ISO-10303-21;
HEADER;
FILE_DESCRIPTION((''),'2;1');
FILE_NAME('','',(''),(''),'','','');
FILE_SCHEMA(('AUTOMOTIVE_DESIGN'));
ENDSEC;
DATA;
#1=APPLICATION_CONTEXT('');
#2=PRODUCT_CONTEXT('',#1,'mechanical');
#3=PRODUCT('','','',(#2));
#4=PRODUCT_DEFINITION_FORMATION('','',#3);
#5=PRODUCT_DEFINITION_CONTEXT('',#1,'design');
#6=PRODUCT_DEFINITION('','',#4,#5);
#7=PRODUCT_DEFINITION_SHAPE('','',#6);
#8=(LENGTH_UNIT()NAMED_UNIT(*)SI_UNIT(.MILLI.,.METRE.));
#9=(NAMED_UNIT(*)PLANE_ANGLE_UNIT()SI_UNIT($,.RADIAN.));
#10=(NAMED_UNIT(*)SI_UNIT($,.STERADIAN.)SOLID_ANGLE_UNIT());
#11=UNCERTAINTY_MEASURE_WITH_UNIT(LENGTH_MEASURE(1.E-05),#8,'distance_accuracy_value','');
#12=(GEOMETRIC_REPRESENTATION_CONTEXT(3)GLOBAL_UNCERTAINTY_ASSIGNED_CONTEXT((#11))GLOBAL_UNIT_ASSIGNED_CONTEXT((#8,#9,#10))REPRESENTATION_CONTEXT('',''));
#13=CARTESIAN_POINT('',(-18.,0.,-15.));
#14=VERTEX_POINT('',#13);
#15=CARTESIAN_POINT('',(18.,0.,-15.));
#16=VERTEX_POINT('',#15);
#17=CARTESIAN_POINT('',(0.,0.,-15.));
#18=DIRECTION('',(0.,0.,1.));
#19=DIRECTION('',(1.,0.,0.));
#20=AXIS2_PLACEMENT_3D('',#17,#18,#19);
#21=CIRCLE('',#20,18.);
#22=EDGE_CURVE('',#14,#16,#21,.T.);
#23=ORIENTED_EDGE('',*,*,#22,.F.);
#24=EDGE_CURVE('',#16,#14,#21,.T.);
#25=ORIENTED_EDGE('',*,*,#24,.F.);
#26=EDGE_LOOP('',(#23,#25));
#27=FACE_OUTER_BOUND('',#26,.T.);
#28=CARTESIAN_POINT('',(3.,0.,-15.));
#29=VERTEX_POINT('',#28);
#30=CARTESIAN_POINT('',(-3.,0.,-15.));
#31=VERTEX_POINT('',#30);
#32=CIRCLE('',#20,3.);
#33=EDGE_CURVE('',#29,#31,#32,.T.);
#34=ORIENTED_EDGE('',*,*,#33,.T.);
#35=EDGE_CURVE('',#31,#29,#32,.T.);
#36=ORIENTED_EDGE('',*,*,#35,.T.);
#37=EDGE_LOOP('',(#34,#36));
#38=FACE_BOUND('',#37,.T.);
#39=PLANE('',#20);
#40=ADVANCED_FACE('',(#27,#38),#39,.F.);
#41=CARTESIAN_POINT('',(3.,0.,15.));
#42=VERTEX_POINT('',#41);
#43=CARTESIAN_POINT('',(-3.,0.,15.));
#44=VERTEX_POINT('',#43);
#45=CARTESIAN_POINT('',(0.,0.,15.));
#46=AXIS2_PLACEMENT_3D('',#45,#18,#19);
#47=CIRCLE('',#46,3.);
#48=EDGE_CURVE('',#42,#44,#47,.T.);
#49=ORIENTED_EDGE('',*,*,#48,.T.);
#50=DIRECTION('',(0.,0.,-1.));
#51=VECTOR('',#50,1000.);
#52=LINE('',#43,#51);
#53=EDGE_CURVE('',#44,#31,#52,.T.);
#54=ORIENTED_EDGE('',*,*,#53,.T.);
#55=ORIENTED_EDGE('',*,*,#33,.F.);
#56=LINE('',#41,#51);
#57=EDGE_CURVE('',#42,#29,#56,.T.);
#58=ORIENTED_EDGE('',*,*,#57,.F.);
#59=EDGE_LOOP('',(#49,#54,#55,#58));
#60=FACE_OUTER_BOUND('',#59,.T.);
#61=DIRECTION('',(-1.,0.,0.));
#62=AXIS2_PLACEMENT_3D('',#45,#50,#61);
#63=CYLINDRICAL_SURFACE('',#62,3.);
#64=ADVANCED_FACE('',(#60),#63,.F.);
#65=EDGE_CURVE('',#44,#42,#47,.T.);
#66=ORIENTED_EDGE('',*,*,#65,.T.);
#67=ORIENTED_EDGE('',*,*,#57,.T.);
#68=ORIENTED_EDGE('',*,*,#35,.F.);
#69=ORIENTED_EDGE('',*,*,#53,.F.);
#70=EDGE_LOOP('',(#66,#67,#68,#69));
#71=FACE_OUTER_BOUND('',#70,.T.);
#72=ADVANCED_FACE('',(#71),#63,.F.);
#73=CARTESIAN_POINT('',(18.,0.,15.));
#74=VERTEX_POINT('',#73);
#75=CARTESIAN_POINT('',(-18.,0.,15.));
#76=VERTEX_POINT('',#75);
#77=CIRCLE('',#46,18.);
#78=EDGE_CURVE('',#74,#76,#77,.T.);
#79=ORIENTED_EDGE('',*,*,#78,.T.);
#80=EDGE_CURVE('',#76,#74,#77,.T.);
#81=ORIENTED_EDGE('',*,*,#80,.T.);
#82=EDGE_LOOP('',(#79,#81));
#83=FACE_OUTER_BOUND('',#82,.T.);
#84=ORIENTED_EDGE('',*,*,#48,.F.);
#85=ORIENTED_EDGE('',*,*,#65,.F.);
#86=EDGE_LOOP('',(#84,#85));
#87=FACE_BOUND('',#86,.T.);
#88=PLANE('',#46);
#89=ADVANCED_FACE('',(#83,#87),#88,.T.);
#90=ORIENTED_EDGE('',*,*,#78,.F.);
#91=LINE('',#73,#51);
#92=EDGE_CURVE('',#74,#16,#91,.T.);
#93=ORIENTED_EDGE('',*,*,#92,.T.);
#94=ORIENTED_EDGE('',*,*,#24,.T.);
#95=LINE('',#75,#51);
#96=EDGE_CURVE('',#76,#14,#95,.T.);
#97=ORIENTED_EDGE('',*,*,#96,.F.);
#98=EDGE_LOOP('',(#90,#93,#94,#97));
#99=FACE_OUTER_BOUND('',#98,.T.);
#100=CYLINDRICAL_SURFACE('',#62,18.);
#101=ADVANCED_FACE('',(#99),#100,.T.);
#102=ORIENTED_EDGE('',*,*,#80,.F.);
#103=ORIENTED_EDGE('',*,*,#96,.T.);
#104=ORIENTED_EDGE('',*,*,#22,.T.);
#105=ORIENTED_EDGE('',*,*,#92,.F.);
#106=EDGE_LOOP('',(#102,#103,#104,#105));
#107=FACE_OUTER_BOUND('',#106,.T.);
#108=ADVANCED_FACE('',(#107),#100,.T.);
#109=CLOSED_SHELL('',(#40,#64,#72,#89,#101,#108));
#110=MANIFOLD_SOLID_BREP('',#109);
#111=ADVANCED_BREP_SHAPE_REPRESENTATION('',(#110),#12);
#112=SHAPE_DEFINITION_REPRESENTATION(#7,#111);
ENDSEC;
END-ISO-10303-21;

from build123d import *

# Parameters (mm, degrees)
BUSHING_PROFILE_36_6_R   = 18
BUSHING_PROFILE_36_6_R_2 = 3
BUSHING_BODY_L30_DEPTH   = 15


with BuildPart() as part:
    # Bushing Profile Ø36-Ø6 → Bushing Body L30 (new, symmetric)
    with BuildSketch(Plane.XY):
        Circle(BUSHING_PROFILE_36_6_R)
        Circle(BUSHING_PROFILE_36_6_R_2, mode=Mode.SUBTRACT)
    extrude(amount=BUSHING_BODY_L30_DEPTH, both=True)


solid = part.part
